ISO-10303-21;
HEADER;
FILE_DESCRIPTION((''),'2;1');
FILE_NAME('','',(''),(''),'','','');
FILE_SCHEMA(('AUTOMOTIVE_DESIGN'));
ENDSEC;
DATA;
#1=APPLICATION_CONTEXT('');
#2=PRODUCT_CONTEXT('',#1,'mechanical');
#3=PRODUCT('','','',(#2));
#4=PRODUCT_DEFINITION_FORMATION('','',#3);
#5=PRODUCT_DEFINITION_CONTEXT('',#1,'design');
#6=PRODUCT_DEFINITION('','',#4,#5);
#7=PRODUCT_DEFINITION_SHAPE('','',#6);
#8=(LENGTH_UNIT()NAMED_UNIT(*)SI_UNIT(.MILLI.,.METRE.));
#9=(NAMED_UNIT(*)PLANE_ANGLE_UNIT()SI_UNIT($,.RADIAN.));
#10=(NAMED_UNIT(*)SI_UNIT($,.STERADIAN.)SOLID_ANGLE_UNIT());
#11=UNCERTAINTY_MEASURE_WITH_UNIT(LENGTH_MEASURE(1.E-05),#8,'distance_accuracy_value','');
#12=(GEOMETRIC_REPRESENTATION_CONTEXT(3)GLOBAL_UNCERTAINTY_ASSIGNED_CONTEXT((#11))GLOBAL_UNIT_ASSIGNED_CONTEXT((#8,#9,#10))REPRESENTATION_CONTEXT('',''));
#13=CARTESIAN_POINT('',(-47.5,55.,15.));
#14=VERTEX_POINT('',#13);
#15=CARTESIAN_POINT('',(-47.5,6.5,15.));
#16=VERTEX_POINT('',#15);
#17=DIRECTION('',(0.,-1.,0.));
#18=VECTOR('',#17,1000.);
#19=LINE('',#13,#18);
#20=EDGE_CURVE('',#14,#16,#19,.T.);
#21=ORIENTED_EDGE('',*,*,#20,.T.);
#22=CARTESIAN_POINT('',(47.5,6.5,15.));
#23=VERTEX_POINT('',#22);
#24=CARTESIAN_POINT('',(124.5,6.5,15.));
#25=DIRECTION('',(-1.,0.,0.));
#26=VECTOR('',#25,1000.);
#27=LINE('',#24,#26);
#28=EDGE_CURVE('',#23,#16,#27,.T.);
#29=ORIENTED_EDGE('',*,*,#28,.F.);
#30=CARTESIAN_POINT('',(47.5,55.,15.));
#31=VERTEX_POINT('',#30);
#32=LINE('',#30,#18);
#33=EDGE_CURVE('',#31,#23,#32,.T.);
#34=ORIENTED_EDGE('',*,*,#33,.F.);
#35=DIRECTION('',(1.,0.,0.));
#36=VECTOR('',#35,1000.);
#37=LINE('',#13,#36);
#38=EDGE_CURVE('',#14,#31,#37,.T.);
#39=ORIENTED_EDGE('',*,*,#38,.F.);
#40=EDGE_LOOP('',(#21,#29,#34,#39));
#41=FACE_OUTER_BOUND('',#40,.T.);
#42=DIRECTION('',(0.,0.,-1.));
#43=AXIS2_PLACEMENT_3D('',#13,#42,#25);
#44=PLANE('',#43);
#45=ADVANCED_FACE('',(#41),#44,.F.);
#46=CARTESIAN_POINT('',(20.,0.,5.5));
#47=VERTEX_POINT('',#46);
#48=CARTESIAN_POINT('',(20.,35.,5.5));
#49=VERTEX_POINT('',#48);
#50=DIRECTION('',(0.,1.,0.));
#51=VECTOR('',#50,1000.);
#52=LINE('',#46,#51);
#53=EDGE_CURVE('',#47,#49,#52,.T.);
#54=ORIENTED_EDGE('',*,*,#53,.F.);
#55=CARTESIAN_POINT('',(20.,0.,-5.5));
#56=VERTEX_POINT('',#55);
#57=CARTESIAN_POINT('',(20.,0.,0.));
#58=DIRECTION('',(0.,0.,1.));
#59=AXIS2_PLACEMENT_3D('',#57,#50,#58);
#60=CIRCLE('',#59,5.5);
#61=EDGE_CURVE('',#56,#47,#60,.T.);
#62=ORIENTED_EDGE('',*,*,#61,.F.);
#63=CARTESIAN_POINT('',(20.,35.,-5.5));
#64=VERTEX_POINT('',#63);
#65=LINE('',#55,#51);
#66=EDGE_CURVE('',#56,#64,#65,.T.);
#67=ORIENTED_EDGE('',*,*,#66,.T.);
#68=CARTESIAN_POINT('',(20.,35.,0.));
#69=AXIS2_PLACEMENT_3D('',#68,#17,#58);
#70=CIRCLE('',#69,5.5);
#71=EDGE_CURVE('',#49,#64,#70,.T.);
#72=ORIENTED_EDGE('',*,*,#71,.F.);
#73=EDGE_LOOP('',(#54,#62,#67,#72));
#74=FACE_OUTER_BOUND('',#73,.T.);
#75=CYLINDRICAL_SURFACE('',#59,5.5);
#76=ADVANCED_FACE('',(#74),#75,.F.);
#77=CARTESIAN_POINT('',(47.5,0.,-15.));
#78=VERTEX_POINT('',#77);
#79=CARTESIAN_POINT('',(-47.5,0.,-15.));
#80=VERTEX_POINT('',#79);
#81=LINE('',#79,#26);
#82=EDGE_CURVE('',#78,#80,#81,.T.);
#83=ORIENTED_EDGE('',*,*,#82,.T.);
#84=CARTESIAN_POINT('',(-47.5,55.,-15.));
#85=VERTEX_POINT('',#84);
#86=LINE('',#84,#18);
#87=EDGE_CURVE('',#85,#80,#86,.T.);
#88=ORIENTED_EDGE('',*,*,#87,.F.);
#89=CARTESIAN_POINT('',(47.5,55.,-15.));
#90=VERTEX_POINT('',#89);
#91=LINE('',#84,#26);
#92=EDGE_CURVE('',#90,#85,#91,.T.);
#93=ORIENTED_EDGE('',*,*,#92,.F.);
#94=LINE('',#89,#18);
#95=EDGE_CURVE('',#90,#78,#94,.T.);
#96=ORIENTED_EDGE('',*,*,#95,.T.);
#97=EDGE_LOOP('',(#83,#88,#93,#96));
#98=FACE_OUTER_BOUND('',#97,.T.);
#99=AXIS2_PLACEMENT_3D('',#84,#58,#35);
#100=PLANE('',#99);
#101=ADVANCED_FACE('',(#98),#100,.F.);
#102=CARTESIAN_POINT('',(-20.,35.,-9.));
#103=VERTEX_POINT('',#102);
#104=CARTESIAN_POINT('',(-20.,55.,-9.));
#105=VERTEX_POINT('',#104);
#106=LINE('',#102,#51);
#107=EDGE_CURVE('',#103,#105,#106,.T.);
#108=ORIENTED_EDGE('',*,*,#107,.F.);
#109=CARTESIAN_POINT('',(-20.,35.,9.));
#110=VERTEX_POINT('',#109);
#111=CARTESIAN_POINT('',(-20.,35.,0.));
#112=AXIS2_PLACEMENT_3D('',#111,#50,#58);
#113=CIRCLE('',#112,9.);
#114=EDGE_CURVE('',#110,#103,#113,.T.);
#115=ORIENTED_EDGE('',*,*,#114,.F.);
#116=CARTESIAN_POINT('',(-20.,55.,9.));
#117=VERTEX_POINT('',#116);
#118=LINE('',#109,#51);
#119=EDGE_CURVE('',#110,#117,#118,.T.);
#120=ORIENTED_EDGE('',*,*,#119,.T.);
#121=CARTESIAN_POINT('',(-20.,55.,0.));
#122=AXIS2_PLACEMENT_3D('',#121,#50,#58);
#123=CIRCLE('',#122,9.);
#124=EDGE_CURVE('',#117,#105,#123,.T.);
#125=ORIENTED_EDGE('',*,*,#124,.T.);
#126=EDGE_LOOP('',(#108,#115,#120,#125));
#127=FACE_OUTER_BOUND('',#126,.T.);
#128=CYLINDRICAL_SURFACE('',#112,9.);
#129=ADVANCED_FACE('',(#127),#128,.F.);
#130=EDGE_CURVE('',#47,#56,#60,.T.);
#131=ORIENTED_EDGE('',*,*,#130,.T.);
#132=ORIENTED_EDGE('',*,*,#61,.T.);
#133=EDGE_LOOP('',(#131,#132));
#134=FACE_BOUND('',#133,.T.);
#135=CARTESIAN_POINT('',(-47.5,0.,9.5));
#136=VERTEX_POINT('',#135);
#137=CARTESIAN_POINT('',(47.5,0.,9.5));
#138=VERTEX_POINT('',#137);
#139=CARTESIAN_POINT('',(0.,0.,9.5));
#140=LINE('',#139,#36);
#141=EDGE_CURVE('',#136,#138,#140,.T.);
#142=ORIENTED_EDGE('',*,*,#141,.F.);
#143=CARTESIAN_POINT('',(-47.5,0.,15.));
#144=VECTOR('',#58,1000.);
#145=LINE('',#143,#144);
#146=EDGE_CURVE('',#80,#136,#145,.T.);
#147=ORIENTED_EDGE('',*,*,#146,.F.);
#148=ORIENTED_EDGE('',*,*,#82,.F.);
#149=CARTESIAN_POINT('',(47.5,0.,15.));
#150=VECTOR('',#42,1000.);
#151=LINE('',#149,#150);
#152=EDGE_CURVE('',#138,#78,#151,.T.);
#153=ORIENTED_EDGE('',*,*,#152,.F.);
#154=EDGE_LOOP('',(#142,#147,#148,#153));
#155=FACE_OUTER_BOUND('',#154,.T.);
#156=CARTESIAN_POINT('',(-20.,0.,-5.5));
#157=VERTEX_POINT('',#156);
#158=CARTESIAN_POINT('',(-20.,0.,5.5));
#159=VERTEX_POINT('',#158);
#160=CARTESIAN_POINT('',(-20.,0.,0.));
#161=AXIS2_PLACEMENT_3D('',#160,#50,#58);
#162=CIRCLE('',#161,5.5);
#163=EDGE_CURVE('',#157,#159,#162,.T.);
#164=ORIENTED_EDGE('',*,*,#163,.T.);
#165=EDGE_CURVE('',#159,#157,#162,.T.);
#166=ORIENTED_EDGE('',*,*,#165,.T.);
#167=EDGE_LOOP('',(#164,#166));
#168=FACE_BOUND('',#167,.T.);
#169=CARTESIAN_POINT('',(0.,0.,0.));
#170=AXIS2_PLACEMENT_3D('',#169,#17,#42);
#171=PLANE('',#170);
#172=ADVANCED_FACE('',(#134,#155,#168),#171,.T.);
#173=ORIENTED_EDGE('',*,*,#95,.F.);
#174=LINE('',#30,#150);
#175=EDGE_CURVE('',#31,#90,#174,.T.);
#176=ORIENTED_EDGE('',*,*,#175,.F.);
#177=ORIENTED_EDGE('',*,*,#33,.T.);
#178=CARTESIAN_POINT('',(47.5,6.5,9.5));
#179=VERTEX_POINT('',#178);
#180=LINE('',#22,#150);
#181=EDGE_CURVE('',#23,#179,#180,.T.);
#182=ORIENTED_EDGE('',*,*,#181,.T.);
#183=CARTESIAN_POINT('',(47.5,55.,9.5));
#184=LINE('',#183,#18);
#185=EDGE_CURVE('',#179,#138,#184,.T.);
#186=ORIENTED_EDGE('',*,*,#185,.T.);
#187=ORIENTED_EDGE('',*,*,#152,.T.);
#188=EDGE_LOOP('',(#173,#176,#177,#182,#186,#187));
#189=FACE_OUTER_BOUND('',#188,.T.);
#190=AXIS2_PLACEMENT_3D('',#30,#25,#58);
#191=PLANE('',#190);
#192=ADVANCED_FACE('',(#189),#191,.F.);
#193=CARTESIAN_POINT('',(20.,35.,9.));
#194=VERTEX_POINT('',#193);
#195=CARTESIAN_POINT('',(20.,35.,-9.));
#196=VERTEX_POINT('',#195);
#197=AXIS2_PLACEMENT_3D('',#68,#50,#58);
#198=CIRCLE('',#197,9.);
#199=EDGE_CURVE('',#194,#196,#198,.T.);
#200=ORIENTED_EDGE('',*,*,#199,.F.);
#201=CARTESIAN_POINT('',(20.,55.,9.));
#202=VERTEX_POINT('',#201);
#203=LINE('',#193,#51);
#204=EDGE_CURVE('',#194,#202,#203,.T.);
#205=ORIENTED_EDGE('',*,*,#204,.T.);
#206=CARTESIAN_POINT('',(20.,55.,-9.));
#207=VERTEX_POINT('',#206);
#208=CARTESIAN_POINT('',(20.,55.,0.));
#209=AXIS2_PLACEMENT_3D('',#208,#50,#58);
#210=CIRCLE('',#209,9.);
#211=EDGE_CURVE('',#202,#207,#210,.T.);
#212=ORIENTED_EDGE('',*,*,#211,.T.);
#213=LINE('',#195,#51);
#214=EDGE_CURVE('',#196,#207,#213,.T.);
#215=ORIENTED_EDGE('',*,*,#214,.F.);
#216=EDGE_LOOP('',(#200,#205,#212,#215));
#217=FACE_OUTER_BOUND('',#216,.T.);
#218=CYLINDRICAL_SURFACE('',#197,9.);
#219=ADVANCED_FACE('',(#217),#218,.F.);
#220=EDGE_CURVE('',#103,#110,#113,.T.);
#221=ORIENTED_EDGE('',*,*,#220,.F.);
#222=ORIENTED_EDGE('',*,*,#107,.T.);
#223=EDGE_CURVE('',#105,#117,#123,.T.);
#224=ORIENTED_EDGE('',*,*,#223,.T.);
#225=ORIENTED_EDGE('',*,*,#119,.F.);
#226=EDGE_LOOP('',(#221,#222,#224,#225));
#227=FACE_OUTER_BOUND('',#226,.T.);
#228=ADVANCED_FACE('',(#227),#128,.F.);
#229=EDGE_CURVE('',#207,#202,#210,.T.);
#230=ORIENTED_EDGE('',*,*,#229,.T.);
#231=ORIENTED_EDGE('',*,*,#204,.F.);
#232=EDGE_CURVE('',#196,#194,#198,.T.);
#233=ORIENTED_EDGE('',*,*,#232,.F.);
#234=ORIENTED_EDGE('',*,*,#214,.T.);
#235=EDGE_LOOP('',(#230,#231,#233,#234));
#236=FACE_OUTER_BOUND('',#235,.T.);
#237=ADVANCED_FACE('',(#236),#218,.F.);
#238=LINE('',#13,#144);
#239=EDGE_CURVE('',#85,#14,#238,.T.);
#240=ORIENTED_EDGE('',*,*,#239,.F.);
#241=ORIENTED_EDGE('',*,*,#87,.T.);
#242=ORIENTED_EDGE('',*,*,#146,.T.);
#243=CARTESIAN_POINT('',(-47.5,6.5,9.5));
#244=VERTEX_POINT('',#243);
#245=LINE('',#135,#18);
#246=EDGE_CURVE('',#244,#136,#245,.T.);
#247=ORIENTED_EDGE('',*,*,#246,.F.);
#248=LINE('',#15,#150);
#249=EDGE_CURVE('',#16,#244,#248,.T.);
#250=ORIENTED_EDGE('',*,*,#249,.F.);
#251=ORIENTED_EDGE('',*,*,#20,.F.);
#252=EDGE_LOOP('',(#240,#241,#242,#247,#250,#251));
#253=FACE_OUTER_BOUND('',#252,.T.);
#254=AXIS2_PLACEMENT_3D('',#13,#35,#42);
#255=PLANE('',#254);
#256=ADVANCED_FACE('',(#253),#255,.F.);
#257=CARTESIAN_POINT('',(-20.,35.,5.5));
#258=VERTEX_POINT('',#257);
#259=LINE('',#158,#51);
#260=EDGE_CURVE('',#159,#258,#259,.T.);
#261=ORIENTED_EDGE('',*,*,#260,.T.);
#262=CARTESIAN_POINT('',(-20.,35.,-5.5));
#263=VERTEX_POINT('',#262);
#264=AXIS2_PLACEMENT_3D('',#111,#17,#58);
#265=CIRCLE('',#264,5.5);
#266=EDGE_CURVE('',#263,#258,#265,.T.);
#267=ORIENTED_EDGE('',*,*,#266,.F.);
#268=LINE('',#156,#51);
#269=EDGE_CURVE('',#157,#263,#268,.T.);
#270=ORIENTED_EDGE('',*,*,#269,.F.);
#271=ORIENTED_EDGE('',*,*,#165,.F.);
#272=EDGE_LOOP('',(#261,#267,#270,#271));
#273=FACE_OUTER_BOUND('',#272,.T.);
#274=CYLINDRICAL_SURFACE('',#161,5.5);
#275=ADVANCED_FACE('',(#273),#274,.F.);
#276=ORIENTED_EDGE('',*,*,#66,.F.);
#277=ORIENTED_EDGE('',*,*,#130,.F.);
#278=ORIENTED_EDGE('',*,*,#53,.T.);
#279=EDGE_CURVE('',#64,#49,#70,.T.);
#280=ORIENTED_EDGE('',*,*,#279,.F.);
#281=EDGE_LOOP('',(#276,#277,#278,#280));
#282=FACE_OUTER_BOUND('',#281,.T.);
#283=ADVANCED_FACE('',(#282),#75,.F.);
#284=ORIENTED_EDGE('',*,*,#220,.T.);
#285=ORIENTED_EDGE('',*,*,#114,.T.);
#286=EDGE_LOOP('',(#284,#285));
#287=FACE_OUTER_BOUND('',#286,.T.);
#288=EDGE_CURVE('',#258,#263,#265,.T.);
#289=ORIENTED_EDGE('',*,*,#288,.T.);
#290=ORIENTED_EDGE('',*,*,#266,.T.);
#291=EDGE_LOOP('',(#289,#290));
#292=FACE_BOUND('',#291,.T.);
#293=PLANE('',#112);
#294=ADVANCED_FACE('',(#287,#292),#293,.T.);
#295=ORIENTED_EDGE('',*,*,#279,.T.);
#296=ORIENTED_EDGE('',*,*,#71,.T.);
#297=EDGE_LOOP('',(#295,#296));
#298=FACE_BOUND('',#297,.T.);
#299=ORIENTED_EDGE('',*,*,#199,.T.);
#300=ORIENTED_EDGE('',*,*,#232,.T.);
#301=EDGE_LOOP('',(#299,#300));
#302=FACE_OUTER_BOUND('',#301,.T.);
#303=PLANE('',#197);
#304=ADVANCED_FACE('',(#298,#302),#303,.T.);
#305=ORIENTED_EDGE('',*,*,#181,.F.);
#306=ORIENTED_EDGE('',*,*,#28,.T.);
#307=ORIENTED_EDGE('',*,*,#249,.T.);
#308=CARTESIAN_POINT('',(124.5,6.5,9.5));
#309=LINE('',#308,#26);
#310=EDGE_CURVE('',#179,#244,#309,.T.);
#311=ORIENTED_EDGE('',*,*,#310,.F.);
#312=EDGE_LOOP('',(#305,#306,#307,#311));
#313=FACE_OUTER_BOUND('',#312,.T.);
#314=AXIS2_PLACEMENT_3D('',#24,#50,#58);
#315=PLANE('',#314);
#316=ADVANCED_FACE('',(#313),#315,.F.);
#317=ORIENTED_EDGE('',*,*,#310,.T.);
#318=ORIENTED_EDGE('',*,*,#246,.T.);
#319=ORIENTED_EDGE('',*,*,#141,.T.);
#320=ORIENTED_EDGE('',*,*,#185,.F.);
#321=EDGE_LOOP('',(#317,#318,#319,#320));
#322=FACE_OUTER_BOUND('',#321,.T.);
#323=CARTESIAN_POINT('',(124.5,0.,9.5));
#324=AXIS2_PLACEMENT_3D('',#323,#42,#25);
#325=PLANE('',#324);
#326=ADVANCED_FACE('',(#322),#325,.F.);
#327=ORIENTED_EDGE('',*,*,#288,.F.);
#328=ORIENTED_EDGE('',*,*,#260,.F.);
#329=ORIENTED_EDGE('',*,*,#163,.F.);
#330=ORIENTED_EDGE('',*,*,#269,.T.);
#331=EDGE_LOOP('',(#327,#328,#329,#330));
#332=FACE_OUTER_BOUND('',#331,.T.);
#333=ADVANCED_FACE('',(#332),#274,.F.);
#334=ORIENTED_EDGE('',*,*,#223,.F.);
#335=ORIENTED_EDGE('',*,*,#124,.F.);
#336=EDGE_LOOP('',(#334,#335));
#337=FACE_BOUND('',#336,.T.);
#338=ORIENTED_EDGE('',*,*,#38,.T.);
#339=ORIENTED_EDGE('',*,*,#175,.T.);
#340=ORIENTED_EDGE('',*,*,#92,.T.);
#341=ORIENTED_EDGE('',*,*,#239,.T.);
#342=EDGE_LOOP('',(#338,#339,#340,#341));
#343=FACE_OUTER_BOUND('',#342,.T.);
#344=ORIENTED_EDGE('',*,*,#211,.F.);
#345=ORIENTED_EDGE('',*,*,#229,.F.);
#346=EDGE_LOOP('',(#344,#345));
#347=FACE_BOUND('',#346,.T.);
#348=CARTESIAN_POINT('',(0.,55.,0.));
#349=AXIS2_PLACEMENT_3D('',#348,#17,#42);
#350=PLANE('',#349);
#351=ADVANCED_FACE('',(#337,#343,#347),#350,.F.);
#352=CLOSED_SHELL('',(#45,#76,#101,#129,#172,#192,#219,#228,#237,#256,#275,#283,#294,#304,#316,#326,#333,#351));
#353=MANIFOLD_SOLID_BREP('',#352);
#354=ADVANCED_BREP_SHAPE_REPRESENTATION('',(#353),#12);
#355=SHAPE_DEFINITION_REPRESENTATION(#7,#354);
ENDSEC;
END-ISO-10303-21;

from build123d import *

# Parameters (mm, degrees)
SKETCH1_W           = 95
SKETCH1_H           = 30
BOSS_EXTRUDE1_DEPTH = 55
SKETCH2_R           = 5.5
CUT_EXTRUDE1_DEPTH  = 75.204110398
SKETCH3_R           = 9
CUT_EXTRUDE2_DEPTH  = 20
SKETCH4_W           = 5.5
SKETCH4_H           = 6.5
CUT_EXTRUDE3_DEPTH  = 172


with BuildPart() as part:
    # Sketch1 → Boss-Extrude1 (new body)
    with BuildSketch(Plane(origin=(0, 0, 0), x_dir=(1, 0, 0), z_dir=(0, 1, 0))):
        Rectangle(SKETCH1_W, SKETCH1_H)
    extrude(amount=BOSS_EXTRUDE1_DEPTH)

    # Sketch2 → Cut-Extrude1 (cut, through all)
    with BuildSketch(Plane(origin=(0, 55, 0), x_dir=(1, 0, 0), z_dir=(0, 1, 0))):
        with Locations(Location((-20, 0, 0), (0, 0, 270))):
            Circle(SKETCH2_R)
        with Locations(Location((20, 0, 0), (0, 0, 270))):
            Circle(SKETCH2_R)
    extrude(amount=-CUT_EXTRUDE1_DEPTH, mode=Mode.SUBTRACT)

    # Sketch3 → Cut-Extrude2 (cut)
    with BuildSketch(Plane(origin=(0, 55, 0), x_dir=(1, 0, 0), z_dir=(0, 1, 0))):
        with Locations(Location((-20, 0, 0), (0, 0, 270))):
            Circle(SKETCH3_R)
        with Locations(Location((20, 0, 0), (0, 0, 270))):
            Circle(SKETCH3_R)
    extrude(amount=-CUT_EXTRUDE2_DEPTH, mode=Mode.SUBTRACT)

    # Sketch4 → Cut-Extrude3 (cut)
    with BuildSketch(Plane.ZY.offset(47.5)):
        with Locations((12.25, 3.25)):
            Rectangle(SKETCH4_W, SKETCH4_H)
    extrude(amount=-CUT_EXTRUDE3_DEPTH, mode=Mode.SUBTRACT)


solid = part.part
